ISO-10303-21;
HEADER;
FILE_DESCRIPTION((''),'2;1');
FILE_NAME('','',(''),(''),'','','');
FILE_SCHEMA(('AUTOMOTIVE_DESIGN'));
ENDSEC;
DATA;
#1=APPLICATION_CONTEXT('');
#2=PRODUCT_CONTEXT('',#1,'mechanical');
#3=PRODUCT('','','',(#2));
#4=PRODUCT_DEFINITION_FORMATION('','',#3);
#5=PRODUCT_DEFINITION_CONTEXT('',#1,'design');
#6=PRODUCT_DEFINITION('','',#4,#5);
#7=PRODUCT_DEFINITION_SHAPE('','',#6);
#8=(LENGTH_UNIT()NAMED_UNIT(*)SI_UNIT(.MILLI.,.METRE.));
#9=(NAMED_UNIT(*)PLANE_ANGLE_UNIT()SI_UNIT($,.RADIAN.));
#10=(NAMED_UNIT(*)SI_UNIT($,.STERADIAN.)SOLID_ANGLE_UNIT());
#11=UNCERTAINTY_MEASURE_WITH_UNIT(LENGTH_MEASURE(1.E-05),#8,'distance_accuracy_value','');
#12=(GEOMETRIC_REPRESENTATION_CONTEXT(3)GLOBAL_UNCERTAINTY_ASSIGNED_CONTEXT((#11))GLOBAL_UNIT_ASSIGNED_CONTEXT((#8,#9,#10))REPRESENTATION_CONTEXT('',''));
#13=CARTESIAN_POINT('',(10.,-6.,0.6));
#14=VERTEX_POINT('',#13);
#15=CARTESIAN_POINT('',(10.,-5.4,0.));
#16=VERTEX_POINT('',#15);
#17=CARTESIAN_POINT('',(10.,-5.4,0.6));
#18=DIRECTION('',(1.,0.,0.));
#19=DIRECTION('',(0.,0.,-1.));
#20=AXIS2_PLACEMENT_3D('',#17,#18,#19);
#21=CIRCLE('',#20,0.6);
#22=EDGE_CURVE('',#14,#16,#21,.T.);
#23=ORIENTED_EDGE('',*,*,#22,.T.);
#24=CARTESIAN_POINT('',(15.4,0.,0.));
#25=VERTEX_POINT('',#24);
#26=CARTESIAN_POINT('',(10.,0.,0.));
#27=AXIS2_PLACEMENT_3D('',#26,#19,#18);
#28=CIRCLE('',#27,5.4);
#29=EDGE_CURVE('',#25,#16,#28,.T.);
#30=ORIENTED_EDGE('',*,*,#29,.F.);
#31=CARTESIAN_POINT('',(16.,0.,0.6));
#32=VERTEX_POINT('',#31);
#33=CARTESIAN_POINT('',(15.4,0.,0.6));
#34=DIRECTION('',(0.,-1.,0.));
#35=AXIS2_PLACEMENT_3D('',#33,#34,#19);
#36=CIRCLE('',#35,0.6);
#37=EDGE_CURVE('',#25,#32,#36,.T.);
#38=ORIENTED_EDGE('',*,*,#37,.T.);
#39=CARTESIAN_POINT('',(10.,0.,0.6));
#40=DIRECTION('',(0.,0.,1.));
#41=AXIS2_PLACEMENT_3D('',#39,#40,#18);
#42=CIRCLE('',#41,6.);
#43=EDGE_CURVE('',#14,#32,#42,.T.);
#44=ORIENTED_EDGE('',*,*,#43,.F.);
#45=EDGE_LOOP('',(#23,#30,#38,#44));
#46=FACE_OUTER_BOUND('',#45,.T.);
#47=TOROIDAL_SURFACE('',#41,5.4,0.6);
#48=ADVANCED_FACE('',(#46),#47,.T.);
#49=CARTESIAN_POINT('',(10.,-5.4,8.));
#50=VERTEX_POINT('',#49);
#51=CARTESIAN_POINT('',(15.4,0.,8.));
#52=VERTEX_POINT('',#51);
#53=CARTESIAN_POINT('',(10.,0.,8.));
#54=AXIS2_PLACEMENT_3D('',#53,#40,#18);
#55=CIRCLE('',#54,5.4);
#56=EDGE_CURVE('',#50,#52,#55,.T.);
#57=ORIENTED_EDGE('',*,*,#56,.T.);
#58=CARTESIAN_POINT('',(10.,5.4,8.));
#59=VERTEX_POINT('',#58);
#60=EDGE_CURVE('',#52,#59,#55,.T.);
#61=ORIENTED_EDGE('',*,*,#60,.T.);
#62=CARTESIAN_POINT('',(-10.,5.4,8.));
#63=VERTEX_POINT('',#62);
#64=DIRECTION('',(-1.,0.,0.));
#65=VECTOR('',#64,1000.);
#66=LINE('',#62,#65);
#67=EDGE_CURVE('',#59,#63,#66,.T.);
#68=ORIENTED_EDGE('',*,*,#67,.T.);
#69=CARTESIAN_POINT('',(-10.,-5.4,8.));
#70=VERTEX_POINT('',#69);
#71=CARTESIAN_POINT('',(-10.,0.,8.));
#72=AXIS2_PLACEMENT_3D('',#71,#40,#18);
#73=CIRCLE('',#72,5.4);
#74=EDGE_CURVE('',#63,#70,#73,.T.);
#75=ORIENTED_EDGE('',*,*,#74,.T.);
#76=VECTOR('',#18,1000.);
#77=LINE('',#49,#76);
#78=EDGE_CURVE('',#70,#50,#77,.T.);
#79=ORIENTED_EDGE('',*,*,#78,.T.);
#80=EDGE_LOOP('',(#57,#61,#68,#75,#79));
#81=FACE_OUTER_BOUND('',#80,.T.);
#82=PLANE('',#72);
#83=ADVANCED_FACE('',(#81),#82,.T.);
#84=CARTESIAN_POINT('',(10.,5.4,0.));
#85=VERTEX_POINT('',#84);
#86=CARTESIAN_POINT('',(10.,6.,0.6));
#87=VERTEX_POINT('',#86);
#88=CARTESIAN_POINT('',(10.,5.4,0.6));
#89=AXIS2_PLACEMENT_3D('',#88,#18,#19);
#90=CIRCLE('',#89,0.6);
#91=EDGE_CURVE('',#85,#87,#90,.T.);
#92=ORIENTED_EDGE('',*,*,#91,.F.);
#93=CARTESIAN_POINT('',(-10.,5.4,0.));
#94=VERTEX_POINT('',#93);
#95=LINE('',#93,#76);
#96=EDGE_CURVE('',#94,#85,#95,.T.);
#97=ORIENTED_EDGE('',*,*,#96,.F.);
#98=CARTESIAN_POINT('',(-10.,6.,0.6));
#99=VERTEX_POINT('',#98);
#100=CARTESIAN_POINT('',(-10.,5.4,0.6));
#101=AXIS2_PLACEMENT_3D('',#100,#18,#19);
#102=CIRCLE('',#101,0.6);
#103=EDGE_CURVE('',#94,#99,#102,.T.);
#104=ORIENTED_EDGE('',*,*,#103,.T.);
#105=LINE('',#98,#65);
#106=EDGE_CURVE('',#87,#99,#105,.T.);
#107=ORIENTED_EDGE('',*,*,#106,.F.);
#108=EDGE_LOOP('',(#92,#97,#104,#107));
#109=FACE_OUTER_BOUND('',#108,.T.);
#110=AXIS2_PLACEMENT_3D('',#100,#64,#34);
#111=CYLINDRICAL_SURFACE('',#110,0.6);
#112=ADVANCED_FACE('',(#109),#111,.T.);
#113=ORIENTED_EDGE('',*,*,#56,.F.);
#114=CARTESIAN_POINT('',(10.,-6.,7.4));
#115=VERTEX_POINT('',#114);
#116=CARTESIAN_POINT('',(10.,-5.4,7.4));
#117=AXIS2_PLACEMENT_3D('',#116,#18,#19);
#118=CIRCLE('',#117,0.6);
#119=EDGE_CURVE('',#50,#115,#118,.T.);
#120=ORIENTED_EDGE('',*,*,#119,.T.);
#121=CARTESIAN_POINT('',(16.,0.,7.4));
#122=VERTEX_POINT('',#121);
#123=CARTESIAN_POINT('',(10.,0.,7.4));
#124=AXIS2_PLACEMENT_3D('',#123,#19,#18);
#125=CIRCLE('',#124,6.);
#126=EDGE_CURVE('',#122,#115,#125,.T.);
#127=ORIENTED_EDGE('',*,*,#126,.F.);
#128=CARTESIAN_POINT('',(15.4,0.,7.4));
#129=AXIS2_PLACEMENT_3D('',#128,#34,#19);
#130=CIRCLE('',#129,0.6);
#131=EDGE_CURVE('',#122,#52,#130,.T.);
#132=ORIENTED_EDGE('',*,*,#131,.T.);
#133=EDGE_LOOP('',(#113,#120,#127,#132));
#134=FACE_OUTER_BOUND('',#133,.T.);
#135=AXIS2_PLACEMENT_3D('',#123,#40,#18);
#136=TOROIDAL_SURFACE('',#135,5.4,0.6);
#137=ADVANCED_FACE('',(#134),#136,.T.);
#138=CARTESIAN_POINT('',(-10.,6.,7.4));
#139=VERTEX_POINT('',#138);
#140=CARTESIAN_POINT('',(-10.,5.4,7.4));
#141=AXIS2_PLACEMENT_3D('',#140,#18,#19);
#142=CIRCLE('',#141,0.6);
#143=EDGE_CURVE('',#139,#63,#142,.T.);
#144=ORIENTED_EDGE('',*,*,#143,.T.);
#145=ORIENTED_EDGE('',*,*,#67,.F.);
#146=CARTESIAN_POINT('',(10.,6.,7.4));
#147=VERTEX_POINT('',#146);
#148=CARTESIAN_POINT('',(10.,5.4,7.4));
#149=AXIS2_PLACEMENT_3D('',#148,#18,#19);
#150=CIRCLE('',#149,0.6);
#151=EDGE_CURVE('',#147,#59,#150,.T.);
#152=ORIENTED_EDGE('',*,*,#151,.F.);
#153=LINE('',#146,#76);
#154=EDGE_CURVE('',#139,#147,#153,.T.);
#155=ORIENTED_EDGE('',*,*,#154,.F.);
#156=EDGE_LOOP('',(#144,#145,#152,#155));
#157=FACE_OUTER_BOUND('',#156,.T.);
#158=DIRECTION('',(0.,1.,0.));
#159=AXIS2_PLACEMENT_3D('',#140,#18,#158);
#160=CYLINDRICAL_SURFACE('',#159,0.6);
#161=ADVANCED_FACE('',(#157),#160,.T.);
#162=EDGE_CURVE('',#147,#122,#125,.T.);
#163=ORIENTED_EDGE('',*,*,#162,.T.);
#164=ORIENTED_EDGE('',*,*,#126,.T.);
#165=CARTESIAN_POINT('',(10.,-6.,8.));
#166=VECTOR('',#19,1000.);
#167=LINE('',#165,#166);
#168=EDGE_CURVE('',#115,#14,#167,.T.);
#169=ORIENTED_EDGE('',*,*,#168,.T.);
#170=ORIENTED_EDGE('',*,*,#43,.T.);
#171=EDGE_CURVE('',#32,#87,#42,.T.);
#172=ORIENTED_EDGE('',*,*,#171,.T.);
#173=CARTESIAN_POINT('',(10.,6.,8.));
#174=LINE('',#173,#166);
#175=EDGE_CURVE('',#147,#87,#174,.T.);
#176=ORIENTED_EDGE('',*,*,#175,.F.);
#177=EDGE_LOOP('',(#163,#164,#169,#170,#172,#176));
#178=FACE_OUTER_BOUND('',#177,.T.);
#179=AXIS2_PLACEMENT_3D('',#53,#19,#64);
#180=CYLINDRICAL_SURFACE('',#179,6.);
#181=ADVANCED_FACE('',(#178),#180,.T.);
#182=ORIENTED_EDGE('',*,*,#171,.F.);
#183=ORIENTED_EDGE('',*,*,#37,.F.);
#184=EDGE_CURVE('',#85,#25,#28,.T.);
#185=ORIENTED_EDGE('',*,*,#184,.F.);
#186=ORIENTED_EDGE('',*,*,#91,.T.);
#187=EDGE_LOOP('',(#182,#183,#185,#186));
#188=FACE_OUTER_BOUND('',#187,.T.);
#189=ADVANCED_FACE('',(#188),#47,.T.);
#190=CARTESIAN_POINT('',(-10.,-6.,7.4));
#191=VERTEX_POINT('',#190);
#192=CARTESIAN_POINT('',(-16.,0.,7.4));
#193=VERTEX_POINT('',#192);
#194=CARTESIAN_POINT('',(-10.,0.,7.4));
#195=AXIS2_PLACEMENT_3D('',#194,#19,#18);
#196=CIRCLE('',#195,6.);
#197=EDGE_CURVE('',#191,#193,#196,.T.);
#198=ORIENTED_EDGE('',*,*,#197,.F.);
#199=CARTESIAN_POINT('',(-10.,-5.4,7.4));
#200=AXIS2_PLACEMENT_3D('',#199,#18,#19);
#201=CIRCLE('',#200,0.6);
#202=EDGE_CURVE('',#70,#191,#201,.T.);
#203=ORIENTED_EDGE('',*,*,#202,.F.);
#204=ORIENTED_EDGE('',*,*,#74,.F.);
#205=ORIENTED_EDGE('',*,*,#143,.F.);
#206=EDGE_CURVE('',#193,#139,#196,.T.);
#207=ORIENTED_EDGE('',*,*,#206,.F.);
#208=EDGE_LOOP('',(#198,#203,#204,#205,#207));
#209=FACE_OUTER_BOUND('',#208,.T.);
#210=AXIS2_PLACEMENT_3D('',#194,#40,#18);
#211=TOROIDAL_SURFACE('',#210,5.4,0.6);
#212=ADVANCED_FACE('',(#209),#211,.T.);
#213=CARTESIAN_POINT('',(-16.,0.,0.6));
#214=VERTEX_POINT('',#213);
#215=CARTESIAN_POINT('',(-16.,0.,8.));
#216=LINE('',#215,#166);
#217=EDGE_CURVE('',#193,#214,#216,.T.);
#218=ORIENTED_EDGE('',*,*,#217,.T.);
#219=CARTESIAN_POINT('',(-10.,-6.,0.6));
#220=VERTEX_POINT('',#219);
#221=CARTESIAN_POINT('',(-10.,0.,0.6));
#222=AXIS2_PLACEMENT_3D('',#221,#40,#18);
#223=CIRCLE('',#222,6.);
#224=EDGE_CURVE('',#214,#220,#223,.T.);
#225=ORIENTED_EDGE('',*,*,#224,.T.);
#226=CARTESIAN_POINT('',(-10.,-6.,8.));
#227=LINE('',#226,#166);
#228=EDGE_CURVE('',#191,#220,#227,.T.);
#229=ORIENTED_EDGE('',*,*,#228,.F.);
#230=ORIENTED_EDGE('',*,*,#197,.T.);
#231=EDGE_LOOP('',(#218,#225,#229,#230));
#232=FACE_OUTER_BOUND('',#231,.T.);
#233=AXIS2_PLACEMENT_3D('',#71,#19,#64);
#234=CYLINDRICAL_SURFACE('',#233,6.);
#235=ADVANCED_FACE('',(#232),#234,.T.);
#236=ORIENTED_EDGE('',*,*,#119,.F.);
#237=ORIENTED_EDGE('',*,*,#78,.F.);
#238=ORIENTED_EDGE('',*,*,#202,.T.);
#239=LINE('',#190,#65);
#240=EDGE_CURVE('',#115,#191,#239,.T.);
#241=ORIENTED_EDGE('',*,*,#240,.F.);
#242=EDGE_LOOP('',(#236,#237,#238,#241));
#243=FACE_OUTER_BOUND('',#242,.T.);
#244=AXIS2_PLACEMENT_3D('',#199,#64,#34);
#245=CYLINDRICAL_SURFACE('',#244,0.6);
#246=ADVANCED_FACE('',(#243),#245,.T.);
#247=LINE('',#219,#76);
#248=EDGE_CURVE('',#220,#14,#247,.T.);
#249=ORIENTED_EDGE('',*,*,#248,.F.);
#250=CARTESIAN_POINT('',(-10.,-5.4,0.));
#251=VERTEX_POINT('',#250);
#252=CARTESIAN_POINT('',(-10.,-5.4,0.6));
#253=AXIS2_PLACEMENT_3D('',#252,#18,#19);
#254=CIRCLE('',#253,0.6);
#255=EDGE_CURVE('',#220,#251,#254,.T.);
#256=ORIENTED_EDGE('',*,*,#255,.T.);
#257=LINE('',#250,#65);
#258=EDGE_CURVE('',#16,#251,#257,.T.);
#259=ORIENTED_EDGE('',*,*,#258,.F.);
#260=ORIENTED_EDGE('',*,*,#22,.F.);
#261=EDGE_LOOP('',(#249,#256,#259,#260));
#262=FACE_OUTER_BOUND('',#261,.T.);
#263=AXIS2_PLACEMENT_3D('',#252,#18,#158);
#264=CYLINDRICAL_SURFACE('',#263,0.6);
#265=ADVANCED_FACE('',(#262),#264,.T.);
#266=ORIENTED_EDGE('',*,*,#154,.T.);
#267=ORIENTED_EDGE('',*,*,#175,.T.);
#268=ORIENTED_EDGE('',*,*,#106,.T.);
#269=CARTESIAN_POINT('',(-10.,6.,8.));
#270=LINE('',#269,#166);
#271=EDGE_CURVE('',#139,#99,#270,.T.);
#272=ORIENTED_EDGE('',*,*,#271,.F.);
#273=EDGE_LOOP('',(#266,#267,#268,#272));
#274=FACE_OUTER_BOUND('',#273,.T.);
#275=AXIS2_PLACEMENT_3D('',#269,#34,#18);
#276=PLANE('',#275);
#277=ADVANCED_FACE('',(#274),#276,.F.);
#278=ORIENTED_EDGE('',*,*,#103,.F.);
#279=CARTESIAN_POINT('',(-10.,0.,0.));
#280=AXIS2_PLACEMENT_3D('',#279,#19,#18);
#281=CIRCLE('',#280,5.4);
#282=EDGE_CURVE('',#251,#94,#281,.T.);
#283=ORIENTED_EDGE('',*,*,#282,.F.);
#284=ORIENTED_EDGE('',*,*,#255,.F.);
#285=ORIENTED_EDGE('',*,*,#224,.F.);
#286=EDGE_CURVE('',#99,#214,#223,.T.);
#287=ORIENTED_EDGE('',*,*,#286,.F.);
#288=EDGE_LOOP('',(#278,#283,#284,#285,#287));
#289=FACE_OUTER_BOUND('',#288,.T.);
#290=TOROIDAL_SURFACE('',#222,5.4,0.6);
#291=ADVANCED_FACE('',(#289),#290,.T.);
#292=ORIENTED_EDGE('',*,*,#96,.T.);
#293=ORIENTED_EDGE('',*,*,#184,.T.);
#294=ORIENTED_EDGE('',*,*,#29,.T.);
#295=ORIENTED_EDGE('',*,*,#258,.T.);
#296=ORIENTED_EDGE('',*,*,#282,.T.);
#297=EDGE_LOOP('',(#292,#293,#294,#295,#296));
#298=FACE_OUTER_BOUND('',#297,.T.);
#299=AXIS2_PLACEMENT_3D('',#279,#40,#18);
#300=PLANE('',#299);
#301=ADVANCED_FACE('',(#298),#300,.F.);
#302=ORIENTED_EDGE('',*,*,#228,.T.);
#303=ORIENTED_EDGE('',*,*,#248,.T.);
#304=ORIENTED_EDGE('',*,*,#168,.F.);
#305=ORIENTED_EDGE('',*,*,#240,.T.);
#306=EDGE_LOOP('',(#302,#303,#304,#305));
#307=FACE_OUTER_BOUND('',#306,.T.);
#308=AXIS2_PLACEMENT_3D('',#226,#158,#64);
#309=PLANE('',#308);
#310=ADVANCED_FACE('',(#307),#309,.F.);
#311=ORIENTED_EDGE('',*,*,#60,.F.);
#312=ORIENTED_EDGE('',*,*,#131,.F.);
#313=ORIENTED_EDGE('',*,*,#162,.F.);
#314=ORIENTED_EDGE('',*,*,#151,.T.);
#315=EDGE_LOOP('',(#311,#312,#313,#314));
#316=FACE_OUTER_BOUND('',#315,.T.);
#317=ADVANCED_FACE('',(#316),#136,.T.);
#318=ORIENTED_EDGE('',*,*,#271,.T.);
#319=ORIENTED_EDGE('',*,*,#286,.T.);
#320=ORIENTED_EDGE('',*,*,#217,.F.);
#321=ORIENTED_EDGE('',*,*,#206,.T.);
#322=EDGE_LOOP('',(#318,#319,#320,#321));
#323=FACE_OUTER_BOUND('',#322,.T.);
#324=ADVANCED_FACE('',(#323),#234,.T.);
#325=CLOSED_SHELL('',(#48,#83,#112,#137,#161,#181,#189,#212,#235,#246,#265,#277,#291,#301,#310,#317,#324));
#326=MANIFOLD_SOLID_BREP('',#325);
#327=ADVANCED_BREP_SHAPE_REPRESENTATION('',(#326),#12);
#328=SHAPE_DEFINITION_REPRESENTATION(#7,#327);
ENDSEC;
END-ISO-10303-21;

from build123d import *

# Parameters (mm, degrees)
EXTRUDE_523_DEPTH = 8
FILLET_1_R        = 0.6


with BuildPart() as part:
    # 草图1 → Extrude 523 (new body)
    with BuildSketch(Plane.XY):
        with BuildLine():
            Line((-10, 6), (10, 6))
            ThreePointArc((10, 6), (16, 0), (10, -6))
            Line((10, -6), (-10, -6))
            ThreePointArc((-10, -6), (-16, 0), (-10, 6))
        make_face()
    extrude(amount=EXTRUDE_523_DEPTH)

    # 圆角1
    fillet_1_edges = [part.edges().sort_by_distance(p)[0] for p in [
        (16, 0, 8),
        (0, 6, 8),
        (-16, 0, 8),
        (0, 6, 0),
        (16, 0, 0),
        (0, -6, 0),
        (-16, 0, 0),
        (0, -6, 8),
    ]]
    fillet(fillet_1_edges, radius=FILLET_1_R)


solid = part.part
